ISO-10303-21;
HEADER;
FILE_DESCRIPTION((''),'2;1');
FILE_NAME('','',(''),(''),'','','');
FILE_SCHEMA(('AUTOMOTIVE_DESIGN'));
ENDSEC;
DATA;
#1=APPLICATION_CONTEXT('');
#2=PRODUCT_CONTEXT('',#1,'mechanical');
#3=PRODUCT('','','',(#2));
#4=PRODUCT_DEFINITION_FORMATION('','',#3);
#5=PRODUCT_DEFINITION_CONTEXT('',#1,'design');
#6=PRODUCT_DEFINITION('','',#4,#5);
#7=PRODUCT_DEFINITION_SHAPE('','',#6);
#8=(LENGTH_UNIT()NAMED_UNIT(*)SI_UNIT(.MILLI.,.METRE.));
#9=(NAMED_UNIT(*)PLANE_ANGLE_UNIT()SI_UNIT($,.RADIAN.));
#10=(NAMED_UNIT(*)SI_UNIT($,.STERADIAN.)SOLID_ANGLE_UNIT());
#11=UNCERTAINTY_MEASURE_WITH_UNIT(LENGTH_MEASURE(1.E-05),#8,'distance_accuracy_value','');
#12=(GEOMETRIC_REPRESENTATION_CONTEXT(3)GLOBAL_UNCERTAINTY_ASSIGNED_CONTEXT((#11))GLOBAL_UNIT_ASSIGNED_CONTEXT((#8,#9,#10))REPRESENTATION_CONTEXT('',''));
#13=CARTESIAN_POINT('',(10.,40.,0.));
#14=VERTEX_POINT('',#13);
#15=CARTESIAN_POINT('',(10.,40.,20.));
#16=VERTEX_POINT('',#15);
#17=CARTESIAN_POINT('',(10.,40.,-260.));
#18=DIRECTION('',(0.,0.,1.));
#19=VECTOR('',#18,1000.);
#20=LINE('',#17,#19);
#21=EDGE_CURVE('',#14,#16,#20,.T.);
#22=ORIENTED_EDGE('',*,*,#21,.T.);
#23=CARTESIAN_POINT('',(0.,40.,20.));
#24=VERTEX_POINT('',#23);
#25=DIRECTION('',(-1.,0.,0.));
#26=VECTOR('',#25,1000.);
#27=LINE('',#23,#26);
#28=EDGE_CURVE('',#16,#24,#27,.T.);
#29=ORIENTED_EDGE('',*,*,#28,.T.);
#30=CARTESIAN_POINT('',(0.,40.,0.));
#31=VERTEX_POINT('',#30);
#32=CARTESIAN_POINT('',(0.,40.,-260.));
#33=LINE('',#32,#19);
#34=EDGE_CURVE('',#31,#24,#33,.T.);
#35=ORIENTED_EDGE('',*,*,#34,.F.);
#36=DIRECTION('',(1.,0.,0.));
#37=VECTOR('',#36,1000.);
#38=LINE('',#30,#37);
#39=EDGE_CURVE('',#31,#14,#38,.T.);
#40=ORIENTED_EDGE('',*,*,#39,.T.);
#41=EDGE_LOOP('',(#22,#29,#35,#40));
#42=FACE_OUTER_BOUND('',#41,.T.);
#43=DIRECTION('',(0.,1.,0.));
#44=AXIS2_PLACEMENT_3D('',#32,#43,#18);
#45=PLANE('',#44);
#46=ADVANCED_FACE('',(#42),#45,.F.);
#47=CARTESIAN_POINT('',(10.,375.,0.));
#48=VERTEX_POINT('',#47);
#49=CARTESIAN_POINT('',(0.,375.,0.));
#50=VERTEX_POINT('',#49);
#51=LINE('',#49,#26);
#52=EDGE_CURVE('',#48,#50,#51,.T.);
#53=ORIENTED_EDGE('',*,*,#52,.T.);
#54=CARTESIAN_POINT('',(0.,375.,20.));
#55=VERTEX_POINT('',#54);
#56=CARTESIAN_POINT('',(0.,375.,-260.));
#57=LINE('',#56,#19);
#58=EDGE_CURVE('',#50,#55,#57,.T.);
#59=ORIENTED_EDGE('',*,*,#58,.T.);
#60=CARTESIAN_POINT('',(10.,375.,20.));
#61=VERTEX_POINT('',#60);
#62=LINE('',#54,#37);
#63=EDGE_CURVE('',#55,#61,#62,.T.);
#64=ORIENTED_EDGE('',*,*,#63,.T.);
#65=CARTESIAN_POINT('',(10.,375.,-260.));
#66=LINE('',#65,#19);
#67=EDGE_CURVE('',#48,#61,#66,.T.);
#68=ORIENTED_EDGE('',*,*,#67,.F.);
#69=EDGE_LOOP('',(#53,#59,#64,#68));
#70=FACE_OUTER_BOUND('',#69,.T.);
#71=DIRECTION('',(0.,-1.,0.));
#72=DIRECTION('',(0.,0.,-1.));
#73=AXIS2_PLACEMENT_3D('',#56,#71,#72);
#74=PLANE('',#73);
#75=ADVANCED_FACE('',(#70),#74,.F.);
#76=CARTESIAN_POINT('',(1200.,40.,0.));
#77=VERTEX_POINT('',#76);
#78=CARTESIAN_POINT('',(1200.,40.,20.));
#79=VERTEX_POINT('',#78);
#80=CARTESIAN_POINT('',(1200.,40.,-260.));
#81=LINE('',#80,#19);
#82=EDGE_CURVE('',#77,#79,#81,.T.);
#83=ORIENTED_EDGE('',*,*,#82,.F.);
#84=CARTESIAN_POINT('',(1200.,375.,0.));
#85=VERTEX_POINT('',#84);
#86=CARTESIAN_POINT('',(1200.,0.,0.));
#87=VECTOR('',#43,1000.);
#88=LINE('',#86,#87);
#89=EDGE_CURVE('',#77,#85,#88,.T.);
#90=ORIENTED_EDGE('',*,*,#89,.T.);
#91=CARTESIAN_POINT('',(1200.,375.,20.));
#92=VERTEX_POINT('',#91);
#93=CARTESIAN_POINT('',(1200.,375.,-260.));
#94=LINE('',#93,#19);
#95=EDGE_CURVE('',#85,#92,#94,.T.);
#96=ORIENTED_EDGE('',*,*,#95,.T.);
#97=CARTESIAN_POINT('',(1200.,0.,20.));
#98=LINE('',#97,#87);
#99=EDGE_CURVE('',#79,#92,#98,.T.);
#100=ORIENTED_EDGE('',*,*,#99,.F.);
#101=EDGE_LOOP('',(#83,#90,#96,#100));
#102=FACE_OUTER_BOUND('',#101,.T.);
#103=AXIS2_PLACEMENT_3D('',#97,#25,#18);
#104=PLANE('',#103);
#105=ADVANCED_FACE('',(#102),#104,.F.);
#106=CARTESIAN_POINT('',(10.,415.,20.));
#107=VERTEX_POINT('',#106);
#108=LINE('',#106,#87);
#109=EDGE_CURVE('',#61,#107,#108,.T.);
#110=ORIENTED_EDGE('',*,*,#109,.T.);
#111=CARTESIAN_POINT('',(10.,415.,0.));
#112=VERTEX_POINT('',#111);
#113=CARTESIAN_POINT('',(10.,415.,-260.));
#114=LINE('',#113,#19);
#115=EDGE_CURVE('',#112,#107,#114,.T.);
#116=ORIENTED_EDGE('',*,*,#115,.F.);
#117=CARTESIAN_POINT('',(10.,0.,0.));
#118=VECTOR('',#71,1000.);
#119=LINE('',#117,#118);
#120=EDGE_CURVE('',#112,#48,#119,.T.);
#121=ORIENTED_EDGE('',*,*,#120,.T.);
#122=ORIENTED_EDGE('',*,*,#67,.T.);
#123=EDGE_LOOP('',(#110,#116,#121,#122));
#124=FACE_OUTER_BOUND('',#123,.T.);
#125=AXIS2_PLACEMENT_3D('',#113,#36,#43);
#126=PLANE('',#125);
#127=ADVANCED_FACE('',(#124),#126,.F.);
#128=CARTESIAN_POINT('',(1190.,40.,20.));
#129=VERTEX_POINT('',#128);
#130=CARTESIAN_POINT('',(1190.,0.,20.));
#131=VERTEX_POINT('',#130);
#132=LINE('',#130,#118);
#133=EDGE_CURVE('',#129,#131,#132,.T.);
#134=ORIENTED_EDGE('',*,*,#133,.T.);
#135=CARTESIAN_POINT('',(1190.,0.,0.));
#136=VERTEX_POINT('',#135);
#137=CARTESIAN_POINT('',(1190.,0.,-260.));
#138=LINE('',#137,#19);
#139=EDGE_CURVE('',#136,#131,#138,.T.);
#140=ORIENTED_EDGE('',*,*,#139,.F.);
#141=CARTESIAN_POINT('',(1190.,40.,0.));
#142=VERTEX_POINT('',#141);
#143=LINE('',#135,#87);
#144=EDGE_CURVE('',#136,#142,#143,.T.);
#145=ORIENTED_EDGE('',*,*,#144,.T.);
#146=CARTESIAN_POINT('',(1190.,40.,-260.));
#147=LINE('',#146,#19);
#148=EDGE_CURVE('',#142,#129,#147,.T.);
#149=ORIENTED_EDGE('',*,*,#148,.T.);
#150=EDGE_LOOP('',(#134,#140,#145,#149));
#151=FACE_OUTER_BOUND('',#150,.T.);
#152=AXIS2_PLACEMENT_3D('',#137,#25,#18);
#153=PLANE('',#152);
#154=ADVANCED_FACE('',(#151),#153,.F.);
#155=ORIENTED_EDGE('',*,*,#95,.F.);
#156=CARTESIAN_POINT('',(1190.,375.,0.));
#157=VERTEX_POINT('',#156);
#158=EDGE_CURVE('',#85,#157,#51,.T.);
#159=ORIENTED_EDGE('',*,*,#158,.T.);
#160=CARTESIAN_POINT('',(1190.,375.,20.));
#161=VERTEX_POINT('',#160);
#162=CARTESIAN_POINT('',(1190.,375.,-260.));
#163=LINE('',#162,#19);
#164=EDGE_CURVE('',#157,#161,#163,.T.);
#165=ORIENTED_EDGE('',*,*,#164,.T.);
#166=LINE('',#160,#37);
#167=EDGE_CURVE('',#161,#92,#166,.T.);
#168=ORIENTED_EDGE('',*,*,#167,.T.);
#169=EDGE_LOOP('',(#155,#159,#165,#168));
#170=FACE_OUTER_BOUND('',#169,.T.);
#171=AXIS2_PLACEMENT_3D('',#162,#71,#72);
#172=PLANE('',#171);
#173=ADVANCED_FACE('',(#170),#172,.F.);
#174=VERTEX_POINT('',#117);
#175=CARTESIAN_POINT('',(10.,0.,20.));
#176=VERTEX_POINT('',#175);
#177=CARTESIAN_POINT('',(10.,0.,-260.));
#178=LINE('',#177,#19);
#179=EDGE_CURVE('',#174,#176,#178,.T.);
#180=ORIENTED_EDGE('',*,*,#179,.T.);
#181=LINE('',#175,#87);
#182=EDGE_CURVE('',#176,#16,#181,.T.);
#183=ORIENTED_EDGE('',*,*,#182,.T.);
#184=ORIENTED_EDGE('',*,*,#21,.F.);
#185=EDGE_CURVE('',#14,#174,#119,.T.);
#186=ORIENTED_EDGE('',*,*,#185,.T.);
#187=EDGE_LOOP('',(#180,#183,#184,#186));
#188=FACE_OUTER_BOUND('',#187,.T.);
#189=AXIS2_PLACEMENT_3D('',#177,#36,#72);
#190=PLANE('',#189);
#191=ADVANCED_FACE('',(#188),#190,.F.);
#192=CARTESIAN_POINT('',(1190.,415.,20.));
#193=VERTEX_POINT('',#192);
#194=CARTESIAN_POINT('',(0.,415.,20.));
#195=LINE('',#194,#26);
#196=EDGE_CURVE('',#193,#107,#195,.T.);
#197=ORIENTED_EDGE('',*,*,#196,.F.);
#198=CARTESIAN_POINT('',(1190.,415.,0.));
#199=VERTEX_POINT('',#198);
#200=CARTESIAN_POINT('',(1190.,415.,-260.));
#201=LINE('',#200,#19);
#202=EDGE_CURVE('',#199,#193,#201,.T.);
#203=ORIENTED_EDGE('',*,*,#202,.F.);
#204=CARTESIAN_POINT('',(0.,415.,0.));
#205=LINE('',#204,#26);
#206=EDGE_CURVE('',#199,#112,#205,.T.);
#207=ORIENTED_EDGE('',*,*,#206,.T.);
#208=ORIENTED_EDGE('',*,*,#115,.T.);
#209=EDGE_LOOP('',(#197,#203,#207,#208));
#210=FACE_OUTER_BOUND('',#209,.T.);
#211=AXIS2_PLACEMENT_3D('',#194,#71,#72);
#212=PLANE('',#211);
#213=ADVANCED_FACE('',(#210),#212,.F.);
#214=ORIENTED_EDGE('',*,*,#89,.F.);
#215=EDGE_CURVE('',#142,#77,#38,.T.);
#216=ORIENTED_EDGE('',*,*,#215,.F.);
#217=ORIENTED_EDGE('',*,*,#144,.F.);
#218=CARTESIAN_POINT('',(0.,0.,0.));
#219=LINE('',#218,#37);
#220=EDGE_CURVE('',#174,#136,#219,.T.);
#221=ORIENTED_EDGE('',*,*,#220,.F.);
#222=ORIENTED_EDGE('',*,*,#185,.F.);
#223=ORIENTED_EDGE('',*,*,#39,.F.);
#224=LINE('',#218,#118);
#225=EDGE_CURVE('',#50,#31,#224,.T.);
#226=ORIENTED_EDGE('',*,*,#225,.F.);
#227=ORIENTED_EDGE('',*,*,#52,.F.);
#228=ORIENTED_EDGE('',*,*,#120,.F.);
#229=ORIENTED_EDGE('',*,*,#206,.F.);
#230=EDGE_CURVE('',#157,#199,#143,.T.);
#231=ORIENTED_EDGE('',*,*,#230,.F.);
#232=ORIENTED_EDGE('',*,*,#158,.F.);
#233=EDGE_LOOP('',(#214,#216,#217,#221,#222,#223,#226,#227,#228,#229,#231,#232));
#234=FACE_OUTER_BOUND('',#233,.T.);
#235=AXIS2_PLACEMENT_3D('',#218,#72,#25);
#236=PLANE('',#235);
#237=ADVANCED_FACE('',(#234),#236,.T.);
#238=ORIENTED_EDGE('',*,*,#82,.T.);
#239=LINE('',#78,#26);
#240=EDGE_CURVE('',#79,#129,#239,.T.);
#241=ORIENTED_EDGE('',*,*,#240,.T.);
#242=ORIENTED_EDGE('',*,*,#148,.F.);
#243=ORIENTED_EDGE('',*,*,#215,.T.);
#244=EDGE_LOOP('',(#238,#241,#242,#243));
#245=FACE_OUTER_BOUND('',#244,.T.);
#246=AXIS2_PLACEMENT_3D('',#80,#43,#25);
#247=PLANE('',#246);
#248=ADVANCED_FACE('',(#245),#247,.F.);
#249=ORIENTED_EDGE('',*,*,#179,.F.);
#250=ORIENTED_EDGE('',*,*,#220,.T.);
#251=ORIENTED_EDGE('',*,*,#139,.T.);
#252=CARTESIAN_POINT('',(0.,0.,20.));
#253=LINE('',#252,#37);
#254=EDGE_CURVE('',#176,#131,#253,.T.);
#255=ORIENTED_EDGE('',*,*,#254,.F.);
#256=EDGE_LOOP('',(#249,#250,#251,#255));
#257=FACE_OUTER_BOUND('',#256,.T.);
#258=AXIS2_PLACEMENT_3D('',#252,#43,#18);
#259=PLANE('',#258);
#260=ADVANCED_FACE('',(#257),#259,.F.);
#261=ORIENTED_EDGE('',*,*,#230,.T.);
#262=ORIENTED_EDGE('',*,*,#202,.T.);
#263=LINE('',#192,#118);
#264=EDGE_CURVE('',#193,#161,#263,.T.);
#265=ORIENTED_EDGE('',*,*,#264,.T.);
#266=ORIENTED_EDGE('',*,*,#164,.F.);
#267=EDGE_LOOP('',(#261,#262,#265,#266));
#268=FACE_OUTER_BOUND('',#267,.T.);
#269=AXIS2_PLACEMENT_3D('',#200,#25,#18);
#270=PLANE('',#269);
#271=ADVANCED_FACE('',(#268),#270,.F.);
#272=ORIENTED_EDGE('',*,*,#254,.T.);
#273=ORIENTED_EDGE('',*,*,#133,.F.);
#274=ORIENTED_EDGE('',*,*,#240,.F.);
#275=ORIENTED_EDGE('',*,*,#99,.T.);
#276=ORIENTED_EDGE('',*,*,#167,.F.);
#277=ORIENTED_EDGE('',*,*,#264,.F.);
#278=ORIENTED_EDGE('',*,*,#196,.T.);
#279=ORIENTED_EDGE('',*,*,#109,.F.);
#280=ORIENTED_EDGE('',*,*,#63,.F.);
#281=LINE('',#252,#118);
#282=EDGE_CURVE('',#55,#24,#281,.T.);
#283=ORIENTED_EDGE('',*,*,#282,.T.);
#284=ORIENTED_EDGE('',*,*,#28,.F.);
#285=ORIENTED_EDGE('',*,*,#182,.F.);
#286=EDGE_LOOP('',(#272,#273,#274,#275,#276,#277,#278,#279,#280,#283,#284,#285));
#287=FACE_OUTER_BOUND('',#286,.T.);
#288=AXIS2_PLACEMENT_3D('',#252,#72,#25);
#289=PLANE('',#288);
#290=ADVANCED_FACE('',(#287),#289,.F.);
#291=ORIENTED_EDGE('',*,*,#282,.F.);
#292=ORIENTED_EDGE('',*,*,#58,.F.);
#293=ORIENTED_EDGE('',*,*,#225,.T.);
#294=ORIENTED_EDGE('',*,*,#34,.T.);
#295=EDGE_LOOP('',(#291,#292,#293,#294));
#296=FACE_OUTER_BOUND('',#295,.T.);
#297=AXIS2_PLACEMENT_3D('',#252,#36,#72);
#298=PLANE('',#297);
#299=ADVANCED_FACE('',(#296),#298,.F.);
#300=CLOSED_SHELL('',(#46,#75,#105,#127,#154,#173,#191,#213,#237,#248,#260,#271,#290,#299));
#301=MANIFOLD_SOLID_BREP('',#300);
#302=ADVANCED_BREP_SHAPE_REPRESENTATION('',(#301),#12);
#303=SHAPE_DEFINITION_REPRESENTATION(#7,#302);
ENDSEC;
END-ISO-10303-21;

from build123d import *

# Parameters (mm, degrees)
SKETCH1_W           = 1200
SKETCH1_H           = 415
BOSS_EXTRUDE1_DEPTH = 20
SKETCH2_W           = 10
SKETCH2_H           = 40
CUT_EXTRUDE1_DEPTH  = 280


with BuildPart() as part:
    # Sketch1 → Boss-Extrude1 (new body)
    with BuildSketch(Plane.XY):
        with Locations((600, 207.5)):
            Rectangle(SKETCH1_W, SKETCH1_H)
    extrude(amount=BOSS_EXTRUDE1_DEPTH)

    # Sketch2 → Cut-Extrude1 (cut)
    with BuildSketch(Plane.XY.offset(20)):
        with Locations((5, 395)):
            Rectangle(SKETCH2_W, SKETCH2_H)
        with Locations((1195, 395)):
            Rectangle(SKETCH2_W, SKETCH2_H)
        with Locations((1195, 20)):
            Rectangle(SKETCH2_W, SKETCH2_H)
        with Locations((5, 20)):
            Rectangle(SKETCH2_W, SKETCH2_H)
    extrude(amount=-CUT_EXTRUDE1_DEPTH, mode=Mode.SUBTRACT)


solid = part.part
